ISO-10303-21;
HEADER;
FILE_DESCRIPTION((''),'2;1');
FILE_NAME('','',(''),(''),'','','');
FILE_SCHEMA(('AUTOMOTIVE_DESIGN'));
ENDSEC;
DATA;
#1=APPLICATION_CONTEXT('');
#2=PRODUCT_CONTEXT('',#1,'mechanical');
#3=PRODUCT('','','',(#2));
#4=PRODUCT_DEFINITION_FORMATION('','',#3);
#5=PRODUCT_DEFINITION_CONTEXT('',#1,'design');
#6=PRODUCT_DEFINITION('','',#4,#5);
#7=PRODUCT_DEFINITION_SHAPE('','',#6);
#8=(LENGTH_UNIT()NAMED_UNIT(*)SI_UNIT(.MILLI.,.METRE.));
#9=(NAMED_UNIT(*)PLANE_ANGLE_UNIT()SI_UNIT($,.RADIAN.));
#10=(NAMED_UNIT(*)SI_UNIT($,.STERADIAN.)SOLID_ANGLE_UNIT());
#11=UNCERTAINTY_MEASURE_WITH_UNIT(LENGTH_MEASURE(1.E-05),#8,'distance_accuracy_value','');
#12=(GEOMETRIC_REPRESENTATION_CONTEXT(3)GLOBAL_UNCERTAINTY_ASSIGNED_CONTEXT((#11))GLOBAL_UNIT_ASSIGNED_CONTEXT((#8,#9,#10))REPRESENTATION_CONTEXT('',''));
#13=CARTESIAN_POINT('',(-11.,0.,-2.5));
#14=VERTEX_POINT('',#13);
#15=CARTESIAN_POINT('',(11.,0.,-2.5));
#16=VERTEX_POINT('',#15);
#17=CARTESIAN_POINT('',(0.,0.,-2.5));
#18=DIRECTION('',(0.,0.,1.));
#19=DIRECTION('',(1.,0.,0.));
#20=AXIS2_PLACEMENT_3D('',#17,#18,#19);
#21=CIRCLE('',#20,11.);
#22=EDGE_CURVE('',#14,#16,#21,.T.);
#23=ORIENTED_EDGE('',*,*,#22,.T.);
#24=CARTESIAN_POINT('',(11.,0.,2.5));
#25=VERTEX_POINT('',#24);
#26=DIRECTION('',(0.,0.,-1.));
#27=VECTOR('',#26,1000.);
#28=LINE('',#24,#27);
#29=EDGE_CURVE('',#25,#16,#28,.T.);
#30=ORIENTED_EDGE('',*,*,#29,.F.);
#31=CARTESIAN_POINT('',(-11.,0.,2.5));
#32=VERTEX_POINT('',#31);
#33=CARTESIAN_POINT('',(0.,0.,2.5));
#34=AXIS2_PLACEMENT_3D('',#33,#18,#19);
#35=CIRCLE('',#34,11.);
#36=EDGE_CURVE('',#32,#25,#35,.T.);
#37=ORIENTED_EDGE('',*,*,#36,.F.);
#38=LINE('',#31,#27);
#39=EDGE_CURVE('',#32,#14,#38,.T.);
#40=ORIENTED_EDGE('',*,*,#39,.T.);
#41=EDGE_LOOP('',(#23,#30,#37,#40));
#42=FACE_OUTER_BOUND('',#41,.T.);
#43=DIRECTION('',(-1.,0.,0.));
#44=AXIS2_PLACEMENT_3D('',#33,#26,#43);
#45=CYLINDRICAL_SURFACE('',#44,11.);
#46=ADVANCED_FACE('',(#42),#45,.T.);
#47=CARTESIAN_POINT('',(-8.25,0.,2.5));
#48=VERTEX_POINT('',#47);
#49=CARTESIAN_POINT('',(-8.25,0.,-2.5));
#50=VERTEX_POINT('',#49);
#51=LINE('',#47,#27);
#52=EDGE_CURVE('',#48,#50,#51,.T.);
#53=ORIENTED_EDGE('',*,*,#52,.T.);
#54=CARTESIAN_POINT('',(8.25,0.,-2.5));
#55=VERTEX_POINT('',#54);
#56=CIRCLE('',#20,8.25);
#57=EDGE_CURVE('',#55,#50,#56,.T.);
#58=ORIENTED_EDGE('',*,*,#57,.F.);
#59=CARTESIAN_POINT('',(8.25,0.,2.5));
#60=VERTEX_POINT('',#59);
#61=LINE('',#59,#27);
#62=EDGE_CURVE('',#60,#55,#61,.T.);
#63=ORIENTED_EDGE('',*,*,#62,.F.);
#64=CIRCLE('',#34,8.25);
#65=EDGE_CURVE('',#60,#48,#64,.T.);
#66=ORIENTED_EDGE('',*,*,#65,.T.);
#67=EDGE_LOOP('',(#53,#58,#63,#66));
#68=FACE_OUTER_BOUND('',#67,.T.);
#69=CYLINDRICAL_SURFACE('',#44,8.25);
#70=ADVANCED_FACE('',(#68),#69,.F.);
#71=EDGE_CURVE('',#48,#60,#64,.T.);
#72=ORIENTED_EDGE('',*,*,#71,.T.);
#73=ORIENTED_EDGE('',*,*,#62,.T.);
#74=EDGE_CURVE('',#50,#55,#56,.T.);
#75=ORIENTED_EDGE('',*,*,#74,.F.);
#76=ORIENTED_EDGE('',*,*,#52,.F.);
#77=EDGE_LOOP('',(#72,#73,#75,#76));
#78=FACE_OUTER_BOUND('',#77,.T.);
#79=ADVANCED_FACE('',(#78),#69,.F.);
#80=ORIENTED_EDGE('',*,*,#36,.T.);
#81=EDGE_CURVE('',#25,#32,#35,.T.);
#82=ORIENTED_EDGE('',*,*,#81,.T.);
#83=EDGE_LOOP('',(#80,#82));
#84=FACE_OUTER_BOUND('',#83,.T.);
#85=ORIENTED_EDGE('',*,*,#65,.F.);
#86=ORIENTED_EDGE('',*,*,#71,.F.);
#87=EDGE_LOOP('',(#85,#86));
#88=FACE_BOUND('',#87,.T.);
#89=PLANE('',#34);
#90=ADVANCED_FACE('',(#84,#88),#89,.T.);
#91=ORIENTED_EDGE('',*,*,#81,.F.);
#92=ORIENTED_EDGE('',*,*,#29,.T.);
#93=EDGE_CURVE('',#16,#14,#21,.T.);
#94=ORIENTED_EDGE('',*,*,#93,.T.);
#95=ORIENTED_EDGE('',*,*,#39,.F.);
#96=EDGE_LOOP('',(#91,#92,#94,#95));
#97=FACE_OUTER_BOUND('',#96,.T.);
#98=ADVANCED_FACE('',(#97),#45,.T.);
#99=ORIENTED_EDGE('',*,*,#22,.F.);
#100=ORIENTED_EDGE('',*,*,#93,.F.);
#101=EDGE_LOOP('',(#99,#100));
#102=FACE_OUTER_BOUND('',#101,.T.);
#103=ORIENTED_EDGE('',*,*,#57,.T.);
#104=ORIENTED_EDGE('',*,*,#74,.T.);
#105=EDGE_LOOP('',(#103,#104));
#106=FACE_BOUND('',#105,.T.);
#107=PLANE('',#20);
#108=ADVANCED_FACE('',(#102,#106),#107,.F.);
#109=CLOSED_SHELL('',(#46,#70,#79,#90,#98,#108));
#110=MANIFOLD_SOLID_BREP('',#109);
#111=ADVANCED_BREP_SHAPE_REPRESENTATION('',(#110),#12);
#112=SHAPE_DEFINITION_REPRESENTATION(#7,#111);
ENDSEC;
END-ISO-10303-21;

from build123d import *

# Parameters (mm, degrees)
SKETCH_1_R      = 11
SKETCH_1_R_2    = 8.25
EXTRUDE_1_DEPTH = 2.5


with BuildPart() as part:
    # 草图1 → 凸台-拉伸1 (new, symmetric)
    with BuildSketch(Plane.XY):
        Circle(SKETCH_1_R)
        Circle(SKETCH_1_R_2, mode=Mode.SUBTRACT)
    extrude(amount=EXTRUDE_1_DEPTH, both=True)


solid = part.part
